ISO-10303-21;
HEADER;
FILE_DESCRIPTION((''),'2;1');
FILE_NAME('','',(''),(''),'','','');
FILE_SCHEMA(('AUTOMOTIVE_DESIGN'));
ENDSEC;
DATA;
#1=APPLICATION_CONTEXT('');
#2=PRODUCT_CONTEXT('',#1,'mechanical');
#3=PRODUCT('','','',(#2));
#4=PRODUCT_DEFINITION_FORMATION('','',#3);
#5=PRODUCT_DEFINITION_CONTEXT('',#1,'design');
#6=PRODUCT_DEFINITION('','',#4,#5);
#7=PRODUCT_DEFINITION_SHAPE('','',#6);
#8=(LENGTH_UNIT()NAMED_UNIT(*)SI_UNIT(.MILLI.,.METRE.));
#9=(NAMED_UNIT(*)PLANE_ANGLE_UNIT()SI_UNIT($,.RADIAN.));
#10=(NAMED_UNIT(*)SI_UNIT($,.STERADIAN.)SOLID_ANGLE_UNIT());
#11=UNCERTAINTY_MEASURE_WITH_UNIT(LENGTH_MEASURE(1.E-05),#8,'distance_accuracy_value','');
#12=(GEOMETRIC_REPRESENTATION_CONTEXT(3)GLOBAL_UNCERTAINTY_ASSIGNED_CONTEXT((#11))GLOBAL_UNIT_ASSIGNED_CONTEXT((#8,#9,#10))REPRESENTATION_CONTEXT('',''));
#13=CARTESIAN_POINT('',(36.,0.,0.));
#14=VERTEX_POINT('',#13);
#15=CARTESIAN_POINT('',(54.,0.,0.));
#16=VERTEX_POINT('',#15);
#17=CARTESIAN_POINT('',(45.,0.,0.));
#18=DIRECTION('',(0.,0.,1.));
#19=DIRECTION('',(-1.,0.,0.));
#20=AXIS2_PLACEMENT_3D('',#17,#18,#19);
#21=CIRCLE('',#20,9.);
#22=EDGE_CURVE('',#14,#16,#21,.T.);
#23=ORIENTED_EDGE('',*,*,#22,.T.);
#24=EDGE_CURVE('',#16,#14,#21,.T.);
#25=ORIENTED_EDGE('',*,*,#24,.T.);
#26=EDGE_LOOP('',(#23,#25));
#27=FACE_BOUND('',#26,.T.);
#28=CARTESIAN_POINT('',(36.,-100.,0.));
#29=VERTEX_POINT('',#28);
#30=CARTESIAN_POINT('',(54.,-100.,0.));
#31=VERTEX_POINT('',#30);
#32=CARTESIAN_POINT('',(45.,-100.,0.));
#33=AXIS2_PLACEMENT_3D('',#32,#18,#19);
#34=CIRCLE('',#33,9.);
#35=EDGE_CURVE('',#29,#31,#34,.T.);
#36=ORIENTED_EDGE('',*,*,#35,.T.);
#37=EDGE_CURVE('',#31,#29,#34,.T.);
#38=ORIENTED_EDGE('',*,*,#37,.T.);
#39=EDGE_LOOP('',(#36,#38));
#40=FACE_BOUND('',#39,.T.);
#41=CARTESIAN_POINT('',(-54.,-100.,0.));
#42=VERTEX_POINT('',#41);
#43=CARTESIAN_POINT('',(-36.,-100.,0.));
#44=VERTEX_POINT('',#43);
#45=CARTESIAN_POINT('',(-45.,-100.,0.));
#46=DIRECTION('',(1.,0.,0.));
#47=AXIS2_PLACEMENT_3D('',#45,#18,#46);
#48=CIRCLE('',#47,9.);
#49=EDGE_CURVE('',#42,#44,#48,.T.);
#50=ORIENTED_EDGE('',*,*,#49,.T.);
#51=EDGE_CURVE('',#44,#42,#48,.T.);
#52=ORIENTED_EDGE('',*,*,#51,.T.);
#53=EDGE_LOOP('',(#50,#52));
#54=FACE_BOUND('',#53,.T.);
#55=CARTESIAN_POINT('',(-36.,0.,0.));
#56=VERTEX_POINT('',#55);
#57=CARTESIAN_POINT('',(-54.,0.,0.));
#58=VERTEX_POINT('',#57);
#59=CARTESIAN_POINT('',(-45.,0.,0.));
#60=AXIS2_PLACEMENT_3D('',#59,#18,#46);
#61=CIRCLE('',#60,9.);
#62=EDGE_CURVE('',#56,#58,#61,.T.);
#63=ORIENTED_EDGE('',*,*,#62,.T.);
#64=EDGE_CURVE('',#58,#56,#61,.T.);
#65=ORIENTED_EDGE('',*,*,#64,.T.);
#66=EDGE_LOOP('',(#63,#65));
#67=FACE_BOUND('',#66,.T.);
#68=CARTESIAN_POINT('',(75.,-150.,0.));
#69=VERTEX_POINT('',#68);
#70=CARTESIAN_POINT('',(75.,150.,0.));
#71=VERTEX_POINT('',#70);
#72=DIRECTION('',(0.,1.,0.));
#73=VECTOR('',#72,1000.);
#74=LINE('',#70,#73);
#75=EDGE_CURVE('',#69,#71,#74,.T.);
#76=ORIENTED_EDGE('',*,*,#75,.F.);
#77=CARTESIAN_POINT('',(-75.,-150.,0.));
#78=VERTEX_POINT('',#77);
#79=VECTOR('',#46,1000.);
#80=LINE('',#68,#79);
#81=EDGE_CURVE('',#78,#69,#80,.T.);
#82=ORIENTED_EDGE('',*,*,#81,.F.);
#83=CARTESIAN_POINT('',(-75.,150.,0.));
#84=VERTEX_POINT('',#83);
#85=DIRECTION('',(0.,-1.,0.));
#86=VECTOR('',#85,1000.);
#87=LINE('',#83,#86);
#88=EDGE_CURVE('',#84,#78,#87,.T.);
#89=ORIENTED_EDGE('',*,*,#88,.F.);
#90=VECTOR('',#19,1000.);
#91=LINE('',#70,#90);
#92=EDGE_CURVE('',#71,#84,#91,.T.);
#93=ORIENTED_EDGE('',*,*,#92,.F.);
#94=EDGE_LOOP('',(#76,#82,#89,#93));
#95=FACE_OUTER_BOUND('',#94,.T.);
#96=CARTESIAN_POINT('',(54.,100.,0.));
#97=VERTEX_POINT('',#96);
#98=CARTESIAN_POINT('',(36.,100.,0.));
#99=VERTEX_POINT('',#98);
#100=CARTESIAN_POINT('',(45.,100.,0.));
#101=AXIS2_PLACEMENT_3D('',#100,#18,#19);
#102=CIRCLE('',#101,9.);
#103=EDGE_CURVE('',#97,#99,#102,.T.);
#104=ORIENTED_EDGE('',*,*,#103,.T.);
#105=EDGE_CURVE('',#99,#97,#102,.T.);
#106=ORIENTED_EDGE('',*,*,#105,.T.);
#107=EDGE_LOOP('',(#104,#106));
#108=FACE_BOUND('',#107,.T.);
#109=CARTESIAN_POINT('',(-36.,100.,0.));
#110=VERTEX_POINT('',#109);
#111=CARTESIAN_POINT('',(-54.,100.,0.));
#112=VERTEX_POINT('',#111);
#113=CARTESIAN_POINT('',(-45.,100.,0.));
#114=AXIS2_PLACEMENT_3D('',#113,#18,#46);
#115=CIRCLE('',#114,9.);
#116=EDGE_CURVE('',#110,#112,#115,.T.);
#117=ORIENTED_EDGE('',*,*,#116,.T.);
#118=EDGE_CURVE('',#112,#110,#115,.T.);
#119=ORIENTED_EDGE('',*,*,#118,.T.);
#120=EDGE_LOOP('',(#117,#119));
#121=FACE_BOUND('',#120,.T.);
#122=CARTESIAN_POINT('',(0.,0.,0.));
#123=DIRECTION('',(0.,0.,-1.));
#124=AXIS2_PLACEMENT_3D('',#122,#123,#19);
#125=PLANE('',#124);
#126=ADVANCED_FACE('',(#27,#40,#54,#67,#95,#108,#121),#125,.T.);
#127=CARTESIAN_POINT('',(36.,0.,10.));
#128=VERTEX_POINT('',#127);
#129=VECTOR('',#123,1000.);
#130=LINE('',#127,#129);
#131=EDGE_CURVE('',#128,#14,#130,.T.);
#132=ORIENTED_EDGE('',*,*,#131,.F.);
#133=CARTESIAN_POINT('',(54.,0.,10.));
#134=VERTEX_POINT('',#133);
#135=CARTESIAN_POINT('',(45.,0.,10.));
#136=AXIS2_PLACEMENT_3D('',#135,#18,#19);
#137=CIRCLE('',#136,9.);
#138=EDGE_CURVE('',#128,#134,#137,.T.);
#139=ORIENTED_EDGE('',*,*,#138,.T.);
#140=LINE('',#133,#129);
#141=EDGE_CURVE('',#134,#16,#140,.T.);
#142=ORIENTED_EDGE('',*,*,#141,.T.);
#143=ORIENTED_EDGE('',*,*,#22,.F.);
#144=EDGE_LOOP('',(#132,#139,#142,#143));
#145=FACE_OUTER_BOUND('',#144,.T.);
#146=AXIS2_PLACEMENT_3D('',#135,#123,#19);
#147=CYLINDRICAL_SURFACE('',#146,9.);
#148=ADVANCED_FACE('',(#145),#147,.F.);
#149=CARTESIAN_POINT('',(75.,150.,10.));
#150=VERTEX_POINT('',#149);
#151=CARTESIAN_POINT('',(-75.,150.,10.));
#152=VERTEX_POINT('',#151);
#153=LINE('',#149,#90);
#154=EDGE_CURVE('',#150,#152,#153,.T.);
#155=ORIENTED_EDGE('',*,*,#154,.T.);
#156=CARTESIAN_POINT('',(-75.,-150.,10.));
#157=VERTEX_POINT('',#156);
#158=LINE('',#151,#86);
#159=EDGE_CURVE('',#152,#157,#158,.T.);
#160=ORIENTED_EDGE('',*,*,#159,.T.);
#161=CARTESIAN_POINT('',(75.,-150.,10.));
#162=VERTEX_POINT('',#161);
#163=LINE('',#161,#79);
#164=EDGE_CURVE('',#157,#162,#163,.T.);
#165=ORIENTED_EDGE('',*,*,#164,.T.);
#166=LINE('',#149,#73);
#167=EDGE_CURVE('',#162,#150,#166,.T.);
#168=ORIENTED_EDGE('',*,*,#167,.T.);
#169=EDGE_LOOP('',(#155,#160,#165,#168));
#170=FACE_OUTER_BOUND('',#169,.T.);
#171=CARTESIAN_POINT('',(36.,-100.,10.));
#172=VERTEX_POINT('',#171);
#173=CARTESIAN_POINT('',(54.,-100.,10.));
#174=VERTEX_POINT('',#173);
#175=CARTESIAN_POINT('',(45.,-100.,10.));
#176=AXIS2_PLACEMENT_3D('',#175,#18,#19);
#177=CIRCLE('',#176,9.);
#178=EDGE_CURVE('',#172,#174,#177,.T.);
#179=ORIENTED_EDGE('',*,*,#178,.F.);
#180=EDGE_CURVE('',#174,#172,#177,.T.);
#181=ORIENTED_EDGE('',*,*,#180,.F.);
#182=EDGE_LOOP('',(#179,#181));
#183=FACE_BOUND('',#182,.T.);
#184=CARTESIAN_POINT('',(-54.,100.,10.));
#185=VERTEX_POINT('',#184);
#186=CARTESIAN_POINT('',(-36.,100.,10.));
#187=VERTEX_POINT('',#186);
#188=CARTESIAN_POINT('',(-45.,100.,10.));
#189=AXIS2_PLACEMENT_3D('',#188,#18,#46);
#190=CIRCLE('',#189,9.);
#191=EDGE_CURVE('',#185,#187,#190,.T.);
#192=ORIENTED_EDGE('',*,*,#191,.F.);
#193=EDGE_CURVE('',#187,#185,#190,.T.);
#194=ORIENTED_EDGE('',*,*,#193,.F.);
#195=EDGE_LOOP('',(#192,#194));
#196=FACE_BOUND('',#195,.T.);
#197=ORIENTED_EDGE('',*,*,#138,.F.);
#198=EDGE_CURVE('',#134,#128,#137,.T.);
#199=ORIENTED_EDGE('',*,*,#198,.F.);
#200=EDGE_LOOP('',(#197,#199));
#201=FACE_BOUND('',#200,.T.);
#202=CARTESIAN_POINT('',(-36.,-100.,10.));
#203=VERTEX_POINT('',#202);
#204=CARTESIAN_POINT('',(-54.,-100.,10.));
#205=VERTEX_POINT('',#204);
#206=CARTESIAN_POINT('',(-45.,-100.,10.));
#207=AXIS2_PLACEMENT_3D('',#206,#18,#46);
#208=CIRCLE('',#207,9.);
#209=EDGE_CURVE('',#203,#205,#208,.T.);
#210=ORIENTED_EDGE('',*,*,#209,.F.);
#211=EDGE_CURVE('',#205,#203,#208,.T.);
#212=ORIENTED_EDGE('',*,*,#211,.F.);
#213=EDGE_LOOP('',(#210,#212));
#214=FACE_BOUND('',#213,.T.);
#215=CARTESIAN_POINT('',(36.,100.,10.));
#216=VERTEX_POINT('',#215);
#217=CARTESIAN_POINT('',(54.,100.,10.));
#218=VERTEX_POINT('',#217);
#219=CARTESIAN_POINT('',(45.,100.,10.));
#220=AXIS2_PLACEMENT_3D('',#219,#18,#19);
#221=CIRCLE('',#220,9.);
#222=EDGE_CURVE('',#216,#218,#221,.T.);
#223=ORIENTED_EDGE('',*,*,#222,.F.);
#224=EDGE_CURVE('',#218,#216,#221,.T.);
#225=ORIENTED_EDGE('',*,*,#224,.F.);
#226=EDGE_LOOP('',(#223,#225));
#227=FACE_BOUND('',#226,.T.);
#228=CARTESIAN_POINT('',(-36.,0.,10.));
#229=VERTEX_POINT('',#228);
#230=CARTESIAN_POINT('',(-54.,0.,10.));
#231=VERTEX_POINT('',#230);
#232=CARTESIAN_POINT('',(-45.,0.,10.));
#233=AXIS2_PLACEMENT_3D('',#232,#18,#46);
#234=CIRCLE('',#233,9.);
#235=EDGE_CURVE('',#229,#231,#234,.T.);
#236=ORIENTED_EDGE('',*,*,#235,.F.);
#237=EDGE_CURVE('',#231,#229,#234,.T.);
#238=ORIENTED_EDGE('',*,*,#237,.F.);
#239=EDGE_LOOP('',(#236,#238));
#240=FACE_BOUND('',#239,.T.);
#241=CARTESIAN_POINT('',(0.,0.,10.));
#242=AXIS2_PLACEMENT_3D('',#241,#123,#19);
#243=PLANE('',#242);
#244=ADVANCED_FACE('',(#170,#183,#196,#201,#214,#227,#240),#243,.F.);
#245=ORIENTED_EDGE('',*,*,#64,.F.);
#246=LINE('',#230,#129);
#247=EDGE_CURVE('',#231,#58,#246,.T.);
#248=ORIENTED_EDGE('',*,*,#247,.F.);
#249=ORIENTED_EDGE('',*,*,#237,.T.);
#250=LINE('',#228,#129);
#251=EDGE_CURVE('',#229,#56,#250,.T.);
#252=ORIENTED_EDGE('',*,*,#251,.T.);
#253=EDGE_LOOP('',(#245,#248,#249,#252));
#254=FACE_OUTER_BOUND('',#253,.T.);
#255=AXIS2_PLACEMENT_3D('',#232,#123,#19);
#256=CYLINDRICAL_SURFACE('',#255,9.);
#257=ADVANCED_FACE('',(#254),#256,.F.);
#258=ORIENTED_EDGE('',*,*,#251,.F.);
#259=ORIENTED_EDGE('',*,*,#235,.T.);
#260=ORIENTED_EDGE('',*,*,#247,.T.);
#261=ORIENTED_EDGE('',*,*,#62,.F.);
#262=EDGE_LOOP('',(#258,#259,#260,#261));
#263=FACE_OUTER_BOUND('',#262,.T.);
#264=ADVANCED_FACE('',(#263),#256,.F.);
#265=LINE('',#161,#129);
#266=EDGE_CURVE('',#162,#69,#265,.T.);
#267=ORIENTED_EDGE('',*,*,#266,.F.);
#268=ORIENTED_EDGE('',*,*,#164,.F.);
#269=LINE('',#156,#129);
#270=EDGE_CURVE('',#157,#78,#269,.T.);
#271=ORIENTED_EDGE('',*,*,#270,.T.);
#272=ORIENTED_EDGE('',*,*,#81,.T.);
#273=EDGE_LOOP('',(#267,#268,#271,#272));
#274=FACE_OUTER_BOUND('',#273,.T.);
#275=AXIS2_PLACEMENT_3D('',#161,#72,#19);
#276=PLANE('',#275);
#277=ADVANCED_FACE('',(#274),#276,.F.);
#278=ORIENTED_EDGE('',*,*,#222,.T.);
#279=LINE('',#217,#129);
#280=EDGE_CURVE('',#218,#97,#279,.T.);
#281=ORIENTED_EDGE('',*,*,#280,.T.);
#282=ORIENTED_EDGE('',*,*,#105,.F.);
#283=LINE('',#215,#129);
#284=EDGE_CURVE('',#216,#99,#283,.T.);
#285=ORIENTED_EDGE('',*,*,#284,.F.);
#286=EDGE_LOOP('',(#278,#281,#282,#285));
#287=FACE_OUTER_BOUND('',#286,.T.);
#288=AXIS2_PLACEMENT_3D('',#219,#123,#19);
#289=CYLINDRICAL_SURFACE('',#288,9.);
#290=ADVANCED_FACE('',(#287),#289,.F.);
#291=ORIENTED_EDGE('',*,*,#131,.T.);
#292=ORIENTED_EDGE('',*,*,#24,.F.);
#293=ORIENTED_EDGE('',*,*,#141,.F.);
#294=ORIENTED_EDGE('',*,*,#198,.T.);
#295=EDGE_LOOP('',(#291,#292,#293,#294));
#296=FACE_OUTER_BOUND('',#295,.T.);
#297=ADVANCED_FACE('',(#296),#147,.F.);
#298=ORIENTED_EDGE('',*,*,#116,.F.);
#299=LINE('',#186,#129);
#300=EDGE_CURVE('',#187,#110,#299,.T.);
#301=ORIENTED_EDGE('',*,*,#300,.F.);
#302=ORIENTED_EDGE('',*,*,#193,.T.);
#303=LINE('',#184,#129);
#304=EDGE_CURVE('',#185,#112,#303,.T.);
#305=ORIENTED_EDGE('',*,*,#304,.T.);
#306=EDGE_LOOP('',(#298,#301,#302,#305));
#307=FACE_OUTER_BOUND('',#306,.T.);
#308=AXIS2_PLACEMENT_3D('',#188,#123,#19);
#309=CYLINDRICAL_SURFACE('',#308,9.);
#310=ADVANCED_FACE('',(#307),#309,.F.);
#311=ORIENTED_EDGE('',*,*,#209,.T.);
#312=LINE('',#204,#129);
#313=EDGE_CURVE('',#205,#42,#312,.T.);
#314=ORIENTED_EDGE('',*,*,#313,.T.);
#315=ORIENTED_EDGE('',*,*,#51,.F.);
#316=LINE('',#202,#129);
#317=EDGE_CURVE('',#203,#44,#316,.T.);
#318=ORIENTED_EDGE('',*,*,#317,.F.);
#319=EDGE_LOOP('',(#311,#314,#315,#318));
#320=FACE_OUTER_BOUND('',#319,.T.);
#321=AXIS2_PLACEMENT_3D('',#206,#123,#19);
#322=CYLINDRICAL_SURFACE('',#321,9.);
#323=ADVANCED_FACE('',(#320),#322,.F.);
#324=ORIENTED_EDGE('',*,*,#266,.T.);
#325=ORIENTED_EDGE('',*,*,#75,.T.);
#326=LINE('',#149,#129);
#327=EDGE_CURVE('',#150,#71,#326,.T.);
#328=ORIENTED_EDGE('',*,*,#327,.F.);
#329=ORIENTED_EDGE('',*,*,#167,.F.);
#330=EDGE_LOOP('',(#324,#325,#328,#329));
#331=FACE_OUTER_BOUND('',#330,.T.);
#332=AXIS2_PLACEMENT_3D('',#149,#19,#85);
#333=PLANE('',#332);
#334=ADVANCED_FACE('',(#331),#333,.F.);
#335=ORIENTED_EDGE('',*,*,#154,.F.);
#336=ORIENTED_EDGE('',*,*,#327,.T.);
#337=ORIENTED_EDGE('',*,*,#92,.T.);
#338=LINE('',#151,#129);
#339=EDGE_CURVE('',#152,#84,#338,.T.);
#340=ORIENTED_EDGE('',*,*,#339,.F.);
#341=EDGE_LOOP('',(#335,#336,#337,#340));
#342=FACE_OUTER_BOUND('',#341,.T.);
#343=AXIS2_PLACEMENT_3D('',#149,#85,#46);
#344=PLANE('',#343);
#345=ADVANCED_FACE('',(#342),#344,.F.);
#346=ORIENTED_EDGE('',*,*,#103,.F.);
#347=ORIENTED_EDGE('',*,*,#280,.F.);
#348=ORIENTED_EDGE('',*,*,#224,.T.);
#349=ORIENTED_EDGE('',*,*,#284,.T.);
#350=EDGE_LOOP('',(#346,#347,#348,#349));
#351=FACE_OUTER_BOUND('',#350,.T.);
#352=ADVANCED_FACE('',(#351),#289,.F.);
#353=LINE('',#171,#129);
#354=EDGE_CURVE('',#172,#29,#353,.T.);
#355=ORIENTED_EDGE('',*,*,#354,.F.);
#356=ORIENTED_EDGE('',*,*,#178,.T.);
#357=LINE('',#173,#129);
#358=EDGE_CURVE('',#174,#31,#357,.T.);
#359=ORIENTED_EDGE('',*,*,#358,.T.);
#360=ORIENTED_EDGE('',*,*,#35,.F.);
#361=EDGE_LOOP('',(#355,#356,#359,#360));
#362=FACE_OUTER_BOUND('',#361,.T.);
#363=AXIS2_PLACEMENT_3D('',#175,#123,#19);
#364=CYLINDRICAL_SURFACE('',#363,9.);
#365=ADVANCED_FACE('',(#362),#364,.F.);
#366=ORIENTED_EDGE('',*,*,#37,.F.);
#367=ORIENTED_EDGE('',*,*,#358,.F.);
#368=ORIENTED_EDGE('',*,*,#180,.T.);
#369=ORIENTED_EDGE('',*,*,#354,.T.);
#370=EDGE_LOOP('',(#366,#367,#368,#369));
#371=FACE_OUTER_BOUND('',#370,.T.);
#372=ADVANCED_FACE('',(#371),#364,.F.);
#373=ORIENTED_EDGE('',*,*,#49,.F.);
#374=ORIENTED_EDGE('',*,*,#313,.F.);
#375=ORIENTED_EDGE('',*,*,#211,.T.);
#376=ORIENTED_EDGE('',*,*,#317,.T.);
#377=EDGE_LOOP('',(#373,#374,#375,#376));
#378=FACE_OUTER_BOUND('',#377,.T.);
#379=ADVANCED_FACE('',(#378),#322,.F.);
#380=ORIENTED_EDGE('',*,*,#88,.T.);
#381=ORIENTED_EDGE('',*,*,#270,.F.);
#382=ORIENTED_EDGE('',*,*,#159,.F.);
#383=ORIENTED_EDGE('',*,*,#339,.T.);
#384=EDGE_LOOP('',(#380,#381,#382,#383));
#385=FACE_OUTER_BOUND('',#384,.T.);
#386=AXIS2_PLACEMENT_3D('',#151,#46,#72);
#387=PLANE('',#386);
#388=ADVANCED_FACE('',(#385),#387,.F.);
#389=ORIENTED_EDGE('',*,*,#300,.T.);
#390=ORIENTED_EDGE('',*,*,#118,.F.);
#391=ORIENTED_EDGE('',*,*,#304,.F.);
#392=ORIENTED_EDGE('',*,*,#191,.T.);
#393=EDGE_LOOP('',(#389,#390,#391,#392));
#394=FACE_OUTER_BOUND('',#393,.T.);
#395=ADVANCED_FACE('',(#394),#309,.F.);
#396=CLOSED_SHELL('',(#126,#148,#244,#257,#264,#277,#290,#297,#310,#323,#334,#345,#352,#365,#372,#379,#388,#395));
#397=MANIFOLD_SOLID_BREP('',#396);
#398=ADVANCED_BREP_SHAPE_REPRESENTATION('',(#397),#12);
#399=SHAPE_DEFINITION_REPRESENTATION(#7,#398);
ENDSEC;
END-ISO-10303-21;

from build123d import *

# Parameters (mm, degrees)
SKETCH1_W           = 150
SKETCH1_H           = 300
SKETCH1_R           = 9
BOSS_EXTRUDE1_DEPTH = 10


with BuildPart() as part:
    # Sketch1 → Boss-Extrude1 (new body)
    with BuildSketch(Plane.XY):
        Rectangle(SKETCH1_W, SKETCH1_H)
        with Locations((-45, 100)):
            Circle(SKETCH1_R, mode=Mode.SUBTRACT)
        with Locations((-45, 0)):
            Circle(SKETCH1_R, mode=Mode.SUBTRACT)
        with Locations((-45, -100)):
            Circle(SKETCH1_R, mode=Mode.SUBTRACT)
        with Locations(Location((45, -100, 0), (0, 0, 180))):
            Circle(SKETCH1_R, mode=Mode.SUBTRACT)
        with Locations(Location((45, 0, 0), (0, 0, 180))):
            Circle(SKETCH1_R, mode=Mode.SUBTRACT)
        with Locations(Location((45, 100, 0), (0, 0, 180))):
            Circle(SKETCH1_R, mode=Mode.SUBTRACT)
    extrude(amount=BOSS_EXTRUDE1_DEPTH)


solid = part.part
